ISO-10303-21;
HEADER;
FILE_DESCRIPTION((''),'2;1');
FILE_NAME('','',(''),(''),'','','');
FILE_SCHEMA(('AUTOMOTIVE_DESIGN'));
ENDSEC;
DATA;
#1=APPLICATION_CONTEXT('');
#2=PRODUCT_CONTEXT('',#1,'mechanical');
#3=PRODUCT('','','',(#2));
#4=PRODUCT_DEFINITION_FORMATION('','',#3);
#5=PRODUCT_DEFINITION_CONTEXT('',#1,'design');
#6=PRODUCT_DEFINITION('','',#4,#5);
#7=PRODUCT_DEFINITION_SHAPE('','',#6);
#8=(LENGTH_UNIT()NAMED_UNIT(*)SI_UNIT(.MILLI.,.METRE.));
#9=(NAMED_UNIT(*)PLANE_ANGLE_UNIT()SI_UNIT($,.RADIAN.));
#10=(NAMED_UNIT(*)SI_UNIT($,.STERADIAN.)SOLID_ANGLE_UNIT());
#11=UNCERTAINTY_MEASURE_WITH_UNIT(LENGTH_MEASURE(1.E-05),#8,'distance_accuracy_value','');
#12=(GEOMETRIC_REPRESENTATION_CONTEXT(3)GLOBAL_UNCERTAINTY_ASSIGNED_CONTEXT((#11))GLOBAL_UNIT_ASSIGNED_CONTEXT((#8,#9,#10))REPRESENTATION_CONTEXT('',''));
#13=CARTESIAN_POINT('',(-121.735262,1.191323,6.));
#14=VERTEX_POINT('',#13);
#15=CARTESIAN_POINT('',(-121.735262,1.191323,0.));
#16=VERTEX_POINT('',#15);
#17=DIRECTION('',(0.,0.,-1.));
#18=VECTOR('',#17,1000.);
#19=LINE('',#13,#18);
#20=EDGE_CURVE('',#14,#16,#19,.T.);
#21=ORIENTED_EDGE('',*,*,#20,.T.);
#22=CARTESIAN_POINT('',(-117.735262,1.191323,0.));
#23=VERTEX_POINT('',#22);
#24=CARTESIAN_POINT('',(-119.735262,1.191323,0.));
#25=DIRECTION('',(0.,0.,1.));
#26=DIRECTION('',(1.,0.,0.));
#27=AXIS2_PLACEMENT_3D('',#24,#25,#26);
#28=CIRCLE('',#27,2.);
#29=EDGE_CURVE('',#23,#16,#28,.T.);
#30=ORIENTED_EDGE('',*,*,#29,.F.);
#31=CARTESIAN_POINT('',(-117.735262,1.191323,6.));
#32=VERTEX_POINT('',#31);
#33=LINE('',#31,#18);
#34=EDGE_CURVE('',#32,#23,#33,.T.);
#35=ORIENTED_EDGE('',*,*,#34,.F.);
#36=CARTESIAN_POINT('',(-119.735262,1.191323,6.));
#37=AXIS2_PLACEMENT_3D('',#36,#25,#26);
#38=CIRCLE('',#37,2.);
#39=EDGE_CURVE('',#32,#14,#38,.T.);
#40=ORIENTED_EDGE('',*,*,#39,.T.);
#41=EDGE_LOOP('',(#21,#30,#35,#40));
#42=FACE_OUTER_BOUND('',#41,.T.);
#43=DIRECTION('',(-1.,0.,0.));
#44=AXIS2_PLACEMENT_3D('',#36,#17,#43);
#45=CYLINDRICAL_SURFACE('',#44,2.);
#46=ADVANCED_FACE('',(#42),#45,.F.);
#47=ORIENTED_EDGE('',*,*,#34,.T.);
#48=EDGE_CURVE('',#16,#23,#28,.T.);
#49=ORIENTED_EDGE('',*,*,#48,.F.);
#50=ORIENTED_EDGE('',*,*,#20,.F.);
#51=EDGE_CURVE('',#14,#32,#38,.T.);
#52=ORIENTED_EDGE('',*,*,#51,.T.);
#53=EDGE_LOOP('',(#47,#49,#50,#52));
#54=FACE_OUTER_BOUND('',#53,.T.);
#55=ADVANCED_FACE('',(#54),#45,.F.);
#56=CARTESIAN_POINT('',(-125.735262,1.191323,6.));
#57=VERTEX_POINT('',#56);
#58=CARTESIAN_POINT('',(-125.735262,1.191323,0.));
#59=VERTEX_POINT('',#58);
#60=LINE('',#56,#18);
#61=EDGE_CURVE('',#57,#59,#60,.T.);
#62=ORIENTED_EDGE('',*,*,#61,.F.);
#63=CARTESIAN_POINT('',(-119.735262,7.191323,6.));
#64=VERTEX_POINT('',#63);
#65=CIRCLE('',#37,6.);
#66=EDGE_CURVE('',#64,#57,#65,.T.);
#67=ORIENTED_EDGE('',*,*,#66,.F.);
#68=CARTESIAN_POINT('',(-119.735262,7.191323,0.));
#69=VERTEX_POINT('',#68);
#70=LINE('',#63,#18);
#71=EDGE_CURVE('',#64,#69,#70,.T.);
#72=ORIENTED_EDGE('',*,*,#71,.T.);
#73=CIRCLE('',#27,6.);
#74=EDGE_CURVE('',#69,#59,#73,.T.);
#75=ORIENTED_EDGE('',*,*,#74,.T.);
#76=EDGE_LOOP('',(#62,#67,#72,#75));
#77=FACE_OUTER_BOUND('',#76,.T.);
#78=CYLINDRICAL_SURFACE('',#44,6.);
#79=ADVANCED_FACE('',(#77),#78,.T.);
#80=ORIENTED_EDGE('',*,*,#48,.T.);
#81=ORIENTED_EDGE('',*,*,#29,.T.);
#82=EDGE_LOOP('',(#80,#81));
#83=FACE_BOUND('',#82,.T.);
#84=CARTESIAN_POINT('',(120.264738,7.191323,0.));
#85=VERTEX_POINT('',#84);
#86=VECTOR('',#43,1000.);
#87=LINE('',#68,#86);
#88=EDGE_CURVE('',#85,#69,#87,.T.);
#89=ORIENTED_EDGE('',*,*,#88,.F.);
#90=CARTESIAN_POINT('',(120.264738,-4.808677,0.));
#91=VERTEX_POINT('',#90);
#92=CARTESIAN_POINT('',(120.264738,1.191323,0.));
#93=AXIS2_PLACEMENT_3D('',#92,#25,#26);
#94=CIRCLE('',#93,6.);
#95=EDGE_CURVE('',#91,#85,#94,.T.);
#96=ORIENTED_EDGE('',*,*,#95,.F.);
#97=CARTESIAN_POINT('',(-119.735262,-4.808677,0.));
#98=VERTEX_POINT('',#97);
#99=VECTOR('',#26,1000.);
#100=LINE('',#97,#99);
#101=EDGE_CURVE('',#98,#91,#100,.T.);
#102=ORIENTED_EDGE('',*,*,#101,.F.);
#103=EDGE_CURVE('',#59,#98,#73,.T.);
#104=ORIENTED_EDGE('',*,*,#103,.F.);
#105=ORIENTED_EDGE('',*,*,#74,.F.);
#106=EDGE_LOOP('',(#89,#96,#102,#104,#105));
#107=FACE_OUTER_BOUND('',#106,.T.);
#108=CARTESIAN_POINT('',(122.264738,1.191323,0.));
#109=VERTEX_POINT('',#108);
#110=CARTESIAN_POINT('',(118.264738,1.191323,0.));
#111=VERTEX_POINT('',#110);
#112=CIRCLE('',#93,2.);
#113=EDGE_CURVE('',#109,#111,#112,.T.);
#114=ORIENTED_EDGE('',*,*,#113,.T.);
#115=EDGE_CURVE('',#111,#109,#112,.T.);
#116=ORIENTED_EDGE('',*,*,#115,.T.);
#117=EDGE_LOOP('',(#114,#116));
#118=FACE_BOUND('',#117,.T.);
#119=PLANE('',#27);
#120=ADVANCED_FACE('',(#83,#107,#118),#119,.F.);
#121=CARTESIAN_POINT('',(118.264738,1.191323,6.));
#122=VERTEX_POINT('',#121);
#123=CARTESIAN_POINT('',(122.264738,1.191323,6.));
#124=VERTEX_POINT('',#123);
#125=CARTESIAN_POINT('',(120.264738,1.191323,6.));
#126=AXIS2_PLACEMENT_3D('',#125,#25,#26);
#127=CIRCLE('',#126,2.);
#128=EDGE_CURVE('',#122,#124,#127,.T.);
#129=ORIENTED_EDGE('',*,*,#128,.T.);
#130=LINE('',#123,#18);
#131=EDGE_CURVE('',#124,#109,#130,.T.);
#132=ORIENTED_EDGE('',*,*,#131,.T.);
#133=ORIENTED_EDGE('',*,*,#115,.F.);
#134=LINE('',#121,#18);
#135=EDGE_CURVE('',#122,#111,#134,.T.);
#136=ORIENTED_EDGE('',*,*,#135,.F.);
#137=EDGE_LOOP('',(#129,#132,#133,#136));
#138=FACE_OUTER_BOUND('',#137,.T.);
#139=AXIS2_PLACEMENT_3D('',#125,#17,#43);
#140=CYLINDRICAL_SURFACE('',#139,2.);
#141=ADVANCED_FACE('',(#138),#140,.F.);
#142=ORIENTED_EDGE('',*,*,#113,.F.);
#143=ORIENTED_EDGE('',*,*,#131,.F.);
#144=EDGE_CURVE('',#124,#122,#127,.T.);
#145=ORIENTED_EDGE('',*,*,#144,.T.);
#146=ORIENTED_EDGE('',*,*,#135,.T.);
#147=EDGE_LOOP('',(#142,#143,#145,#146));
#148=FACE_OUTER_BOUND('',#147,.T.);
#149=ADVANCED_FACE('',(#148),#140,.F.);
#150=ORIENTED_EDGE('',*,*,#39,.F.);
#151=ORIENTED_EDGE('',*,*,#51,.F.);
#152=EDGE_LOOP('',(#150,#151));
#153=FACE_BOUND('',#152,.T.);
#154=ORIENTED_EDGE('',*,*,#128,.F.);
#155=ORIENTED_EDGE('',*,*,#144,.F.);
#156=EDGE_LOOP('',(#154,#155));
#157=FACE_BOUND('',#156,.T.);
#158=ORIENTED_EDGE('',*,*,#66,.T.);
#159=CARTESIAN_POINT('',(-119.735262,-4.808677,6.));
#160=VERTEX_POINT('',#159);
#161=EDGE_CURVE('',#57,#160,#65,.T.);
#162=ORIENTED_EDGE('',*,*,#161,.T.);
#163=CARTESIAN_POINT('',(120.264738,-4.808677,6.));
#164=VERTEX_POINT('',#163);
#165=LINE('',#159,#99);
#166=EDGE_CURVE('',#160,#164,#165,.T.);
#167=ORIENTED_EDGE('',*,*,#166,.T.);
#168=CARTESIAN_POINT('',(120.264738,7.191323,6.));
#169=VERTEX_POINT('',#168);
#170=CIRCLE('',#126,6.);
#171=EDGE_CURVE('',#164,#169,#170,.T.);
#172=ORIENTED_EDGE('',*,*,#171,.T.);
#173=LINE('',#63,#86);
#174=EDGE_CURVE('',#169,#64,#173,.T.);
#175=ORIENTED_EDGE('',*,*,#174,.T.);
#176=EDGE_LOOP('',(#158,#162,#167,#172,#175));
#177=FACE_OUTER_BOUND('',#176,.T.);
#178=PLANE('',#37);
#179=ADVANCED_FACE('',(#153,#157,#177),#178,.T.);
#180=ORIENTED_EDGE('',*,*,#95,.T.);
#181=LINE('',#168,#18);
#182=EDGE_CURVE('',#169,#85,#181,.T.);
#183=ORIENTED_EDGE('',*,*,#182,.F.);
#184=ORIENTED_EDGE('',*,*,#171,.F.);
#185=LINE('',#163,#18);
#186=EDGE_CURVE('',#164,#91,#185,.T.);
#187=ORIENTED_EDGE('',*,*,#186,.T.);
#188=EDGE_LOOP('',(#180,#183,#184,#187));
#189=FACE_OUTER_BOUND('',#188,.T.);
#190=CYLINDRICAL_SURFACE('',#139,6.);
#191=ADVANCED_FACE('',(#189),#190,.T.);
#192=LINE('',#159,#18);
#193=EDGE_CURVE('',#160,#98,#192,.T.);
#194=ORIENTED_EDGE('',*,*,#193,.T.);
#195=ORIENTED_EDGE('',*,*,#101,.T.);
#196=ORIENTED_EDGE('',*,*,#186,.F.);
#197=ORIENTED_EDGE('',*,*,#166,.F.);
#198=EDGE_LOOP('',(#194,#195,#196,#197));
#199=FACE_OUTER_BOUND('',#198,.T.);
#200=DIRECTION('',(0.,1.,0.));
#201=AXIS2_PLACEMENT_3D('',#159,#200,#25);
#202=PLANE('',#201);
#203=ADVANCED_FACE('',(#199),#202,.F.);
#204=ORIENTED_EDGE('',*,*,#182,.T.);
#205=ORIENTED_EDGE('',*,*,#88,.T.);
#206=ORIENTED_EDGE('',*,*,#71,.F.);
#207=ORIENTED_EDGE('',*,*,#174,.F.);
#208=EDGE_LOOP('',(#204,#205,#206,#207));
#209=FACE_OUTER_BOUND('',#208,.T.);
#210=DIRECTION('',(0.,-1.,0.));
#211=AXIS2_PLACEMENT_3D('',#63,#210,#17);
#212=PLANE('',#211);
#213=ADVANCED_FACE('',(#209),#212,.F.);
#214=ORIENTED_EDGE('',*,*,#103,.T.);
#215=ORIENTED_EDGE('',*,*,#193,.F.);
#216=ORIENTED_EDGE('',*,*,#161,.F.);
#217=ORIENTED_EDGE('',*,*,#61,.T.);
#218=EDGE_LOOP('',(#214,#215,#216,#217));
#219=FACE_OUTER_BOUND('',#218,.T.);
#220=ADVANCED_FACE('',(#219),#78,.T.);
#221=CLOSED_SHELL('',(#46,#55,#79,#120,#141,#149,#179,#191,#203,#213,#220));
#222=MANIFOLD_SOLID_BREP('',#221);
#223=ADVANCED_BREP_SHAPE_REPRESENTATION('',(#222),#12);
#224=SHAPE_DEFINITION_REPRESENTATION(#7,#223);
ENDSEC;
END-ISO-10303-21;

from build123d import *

# Parameters (mm, degrees)
SKETCH_1_R      = 2
EXTRUDE_1_DEPTH = 6


with BuildPart() as part:
    # 草图1 → 凸台-拉伸1 (new body)
    with BuildSketch(Plane.XY):
        with BuildLine():
            Line((-119.735261546, 7.191323041), (120.264738454, 7.191323041))
            ThreePointArc((120.264738454, 7.191323041), (126.264738454, 1.191323041), (120.264738454, -4.808676959))
            Line((120.264738454, -4.808676959), (-119.735261546, -4.808676959))
            ThreePointArc((-119.735261546, -4.808676959), (-125.735261546, 1.191323041), (-119.735261546, 7.191323041))
        make_face()
        with Locations((-119.735261546, 1.191323041)):
            Circle(SKETCH_1_R, mode=Mode.SUBTRACT)
        with Locations((120.264738454, 1.191323041)):
            Circle(SKETCH_1_R, mode=Mode.SUBTRACT)
    extrude(amount=EXTRUDE_1_DEPTH)


solid = part.part
